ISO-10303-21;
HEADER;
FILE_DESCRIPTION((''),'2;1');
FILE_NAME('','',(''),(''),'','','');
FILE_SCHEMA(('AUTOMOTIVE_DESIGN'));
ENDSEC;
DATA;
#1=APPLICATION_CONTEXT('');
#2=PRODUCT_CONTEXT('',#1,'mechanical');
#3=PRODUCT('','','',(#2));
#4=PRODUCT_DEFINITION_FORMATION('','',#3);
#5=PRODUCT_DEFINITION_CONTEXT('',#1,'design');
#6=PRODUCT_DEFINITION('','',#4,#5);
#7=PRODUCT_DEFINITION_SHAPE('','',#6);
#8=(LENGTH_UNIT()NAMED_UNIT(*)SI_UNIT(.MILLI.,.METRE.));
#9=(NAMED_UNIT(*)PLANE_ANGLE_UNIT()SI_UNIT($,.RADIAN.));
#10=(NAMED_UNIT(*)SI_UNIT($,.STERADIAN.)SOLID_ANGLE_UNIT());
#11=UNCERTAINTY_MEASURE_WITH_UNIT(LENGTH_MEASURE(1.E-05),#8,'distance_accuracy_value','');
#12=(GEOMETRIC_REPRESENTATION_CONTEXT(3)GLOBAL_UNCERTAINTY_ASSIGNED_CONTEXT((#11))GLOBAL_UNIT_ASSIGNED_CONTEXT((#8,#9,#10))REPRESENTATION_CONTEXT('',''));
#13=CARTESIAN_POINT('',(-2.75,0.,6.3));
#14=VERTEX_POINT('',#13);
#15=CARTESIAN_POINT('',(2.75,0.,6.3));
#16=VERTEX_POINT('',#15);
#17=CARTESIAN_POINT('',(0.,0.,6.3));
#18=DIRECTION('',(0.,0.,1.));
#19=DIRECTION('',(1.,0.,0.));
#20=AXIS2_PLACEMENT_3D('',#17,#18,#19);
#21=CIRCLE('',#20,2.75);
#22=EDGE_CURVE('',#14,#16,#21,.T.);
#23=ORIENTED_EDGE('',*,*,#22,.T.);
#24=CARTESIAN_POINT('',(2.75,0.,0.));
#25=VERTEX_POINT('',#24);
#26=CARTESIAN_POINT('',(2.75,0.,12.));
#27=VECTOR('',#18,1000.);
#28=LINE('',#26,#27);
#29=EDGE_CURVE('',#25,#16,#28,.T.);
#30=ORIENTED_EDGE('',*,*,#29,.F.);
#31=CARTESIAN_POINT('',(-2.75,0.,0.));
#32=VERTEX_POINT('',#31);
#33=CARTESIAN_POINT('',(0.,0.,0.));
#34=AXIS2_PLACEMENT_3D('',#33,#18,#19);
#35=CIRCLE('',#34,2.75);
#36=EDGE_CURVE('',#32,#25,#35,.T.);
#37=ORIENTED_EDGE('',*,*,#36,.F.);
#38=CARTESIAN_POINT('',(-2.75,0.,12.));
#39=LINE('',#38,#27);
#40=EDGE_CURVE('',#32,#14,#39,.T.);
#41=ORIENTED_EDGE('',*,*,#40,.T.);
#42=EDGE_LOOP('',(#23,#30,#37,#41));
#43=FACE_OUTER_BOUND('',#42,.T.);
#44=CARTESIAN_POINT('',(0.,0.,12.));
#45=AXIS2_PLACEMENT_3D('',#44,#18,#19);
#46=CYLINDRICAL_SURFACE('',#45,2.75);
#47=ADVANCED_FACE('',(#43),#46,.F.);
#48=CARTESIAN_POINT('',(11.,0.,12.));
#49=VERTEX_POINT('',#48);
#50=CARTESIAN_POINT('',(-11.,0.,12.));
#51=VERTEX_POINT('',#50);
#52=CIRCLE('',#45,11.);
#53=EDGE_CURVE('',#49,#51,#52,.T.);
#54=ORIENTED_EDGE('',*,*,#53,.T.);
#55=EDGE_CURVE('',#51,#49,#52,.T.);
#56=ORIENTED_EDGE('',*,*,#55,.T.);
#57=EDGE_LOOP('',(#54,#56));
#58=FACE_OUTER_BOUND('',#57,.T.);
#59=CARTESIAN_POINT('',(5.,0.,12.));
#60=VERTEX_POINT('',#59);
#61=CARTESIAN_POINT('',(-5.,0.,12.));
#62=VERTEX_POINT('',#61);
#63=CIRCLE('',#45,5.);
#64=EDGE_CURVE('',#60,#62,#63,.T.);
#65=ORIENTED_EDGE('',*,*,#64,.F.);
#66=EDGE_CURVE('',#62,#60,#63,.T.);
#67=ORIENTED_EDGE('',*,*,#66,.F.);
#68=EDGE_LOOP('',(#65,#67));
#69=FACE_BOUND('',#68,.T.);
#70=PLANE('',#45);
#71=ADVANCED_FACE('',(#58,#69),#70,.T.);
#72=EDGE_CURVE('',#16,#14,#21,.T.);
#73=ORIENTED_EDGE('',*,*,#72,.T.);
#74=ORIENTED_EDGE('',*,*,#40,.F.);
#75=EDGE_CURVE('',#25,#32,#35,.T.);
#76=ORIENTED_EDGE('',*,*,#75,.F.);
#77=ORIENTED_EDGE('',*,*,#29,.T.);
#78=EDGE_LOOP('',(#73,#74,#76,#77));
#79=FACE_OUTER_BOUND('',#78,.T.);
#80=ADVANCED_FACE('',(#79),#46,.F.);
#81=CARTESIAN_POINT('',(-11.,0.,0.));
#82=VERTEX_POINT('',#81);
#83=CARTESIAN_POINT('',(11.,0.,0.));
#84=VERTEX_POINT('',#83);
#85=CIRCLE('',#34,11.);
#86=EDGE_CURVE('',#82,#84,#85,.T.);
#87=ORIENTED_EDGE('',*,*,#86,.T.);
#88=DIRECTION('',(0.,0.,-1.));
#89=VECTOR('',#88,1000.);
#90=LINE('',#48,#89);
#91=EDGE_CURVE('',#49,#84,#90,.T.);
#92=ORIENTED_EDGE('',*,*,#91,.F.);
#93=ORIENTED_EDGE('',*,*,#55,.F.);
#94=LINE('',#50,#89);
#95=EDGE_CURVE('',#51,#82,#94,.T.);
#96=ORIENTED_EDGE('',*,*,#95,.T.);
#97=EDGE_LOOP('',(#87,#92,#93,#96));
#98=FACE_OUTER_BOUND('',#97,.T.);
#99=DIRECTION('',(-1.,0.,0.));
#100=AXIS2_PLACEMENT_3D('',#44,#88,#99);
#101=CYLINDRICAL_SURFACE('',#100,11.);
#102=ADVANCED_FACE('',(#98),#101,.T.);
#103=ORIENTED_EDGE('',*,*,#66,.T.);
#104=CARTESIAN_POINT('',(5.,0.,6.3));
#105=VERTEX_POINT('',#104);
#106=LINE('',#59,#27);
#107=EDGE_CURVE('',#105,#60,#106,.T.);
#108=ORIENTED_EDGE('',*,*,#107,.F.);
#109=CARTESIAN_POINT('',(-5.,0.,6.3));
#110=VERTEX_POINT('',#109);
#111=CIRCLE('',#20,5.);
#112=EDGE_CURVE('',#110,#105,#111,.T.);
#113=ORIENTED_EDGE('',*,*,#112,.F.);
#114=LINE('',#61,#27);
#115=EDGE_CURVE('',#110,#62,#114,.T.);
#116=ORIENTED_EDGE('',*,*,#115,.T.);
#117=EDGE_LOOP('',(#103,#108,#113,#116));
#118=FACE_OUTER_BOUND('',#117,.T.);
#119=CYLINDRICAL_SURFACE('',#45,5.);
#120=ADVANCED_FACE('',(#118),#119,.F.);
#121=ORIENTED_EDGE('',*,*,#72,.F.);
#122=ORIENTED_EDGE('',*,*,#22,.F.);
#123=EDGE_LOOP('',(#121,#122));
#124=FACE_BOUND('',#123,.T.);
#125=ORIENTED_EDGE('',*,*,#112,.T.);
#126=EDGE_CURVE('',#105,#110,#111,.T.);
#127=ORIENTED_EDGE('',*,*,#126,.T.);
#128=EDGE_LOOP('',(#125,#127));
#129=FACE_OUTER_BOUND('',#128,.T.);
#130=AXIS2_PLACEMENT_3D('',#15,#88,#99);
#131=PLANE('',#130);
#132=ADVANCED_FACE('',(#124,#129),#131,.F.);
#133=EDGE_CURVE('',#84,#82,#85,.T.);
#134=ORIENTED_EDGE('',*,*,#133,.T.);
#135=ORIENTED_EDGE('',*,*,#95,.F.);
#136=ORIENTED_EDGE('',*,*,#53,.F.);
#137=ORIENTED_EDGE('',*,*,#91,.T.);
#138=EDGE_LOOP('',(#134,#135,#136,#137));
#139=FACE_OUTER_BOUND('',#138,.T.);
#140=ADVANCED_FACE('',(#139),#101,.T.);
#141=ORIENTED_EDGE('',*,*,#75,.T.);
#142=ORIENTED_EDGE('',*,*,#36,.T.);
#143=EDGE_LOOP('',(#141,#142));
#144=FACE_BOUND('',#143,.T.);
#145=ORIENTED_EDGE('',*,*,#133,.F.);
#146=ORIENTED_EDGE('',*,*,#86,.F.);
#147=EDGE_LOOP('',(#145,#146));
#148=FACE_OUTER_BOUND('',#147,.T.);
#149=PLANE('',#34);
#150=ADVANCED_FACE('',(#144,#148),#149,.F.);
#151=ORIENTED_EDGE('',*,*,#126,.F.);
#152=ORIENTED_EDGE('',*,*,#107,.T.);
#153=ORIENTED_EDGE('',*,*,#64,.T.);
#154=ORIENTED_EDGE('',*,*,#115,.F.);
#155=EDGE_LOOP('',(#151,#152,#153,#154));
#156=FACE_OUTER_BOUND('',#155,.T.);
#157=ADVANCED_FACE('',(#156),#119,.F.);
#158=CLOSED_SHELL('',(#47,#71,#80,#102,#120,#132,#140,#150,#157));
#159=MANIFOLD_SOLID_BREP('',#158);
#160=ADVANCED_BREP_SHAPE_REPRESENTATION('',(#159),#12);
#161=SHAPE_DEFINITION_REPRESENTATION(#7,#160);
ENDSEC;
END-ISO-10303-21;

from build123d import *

# Parameters (mm, degrees)
SKETCH_1_R                = 11
EXTRUDE_1_DEPTH           = 12
HOLE_WIZARD_1_D           = 5.5
HOLE_WIZARD_1_CBORE_D     = 10
HOLE_WIZARD_1_CBORE_DEPTH = 5.7


with BuildPart() as part:
    # 草图1 → 凸台-拉伸1 (new body)
    with BuildSketch(Plane.XY):
        Circle(SKETCH_1_R)
    extrude(amount=EXTRUDE_1_DEPTH)

    # 打孔尺寸(%根据)内六角圆柱头螺钉的类型1 (through all)
    with Locations(Plane.XY.offset(12)):
        with Locations((0, 0)):
            CounterBoreHole(HOLE_WIZARD_1_D / 2, HOLE_WIZARD_1_CBORE_D / 2, HOLE_WIZARD_1_CBORE_DEPTH)


solid = part.part
